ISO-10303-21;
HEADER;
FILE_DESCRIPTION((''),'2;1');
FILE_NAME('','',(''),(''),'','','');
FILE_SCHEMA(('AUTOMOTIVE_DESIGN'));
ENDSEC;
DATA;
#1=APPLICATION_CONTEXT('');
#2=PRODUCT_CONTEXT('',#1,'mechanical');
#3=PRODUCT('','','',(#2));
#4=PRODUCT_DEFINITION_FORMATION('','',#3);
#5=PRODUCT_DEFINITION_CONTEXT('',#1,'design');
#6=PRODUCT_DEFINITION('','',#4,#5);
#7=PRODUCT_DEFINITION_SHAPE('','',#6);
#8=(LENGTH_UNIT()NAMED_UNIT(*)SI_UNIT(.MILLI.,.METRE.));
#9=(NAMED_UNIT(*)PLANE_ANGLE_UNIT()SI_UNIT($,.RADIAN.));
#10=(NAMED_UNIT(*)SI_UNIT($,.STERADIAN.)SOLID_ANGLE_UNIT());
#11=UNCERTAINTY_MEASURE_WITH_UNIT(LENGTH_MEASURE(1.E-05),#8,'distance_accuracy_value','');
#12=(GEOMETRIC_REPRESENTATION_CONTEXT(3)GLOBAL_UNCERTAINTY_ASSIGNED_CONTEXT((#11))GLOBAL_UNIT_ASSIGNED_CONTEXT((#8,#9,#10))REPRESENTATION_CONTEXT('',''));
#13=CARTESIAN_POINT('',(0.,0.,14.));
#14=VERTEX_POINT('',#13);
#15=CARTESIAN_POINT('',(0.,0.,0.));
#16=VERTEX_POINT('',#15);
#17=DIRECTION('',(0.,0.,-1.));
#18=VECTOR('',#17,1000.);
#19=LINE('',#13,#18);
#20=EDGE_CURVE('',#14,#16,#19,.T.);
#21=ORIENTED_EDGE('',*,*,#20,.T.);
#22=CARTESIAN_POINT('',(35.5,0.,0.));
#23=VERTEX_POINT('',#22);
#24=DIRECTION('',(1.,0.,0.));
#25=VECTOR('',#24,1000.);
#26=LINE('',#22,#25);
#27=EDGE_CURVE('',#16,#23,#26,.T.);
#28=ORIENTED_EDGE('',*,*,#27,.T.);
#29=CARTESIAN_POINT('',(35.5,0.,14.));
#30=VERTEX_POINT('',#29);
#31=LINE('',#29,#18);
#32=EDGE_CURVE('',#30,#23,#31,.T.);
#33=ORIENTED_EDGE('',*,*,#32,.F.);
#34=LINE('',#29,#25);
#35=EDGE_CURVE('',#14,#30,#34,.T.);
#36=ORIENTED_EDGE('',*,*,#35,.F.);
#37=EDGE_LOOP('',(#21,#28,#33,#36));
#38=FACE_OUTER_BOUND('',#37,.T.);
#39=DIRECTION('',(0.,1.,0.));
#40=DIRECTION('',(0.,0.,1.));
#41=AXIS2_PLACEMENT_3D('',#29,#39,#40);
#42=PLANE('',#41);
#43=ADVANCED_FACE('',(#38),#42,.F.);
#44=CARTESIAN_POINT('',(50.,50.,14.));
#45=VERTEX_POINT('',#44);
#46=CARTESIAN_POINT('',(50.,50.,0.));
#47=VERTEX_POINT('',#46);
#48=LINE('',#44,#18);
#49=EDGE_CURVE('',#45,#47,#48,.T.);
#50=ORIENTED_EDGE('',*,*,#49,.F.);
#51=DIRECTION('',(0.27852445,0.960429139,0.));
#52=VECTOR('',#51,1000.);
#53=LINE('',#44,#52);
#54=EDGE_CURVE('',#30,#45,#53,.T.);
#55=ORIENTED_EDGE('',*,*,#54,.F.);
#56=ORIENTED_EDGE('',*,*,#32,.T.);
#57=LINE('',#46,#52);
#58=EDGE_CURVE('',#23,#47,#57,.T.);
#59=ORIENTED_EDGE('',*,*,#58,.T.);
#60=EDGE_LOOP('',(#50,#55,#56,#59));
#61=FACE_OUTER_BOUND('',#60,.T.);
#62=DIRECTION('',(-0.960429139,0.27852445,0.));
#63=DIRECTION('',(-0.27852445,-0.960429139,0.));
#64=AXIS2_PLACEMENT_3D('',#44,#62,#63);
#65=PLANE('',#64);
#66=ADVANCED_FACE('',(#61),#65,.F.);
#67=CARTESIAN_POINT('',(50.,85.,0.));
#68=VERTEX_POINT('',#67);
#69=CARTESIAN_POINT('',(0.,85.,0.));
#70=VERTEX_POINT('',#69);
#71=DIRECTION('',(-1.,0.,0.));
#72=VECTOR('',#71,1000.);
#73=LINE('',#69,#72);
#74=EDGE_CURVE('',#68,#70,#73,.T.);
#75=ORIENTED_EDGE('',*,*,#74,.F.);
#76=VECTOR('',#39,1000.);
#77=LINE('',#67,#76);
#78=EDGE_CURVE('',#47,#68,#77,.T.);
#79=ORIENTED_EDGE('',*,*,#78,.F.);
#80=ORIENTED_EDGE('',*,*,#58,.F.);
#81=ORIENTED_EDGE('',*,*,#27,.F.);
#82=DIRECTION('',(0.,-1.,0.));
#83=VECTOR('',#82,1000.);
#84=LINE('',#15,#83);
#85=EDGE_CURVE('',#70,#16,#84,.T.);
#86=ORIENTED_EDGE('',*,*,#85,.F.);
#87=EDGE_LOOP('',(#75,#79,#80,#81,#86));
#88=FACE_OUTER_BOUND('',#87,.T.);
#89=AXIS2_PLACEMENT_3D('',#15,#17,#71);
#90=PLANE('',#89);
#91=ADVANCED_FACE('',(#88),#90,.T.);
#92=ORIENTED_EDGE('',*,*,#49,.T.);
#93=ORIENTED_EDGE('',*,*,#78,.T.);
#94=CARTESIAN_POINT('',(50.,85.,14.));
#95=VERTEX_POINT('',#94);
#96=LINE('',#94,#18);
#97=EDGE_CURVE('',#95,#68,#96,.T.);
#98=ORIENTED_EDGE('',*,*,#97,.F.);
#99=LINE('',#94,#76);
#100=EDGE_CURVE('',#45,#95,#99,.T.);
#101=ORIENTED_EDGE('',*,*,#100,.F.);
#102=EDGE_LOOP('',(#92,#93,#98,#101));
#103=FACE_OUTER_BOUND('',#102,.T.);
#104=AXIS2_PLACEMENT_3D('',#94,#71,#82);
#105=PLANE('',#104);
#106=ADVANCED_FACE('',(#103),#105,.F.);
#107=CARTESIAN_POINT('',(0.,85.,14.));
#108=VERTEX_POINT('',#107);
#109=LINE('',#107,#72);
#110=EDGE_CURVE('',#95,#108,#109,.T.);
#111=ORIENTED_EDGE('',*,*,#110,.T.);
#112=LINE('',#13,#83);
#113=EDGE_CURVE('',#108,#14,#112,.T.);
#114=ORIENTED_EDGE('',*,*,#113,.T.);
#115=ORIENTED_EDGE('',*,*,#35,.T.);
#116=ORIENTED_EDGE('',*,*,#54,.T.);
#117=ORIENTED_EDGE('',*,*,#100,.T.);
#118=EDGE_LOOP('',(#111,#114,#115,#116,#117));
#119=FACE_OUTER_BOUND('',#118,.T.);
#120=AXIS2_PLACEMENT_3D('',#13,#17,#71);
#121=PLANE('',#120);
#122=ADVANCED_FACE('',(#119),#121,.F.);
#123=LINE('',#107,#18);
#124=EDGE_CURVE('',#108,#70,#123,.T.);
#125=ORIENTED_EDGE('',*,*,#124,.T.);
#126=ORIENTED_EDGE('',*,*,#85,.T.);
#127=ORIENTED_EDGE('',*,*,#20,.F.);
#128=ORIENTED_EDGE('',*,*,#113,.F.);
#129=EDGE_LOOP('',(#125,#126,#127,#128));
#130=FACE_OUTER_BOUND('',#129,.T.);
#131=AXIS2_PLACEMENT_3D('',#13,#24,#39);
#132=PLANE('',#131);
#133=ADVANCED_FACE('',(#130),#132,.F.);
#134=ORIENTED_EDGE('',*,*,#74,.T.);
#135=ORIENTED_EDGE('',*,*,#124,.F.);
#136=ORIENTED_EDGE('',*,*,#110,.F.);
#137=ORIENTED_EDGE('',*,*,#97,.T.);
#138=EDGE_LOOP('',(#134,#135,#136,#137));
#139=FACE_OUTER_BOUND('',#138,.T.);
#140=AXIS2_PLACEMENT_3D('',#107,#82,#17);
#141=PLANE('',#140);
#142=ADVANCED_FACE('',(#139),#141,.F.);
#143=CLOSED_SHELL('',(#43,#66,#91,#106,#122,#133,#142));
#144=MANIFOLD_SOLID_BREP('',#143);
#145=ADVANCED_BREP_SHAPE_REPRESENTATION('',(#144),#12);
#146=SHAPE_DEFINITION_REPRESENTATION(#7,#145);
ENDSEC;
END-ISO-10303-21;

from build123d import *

# Parameters (mm, degrees)
EXTRUDE_1_DEPTH = 14


with BuildPart() as part:
    # 草图1 → 凸台-拉伸1 (new body)
    with BuildSketch(Plane.XY):
        Polygon((0, 0), (0, 85), (50, 85), (50, 50), (35.5, 0), align=None)
    extrude(amount=EXTRUDE_1_DEPTH)


solid = part.part
